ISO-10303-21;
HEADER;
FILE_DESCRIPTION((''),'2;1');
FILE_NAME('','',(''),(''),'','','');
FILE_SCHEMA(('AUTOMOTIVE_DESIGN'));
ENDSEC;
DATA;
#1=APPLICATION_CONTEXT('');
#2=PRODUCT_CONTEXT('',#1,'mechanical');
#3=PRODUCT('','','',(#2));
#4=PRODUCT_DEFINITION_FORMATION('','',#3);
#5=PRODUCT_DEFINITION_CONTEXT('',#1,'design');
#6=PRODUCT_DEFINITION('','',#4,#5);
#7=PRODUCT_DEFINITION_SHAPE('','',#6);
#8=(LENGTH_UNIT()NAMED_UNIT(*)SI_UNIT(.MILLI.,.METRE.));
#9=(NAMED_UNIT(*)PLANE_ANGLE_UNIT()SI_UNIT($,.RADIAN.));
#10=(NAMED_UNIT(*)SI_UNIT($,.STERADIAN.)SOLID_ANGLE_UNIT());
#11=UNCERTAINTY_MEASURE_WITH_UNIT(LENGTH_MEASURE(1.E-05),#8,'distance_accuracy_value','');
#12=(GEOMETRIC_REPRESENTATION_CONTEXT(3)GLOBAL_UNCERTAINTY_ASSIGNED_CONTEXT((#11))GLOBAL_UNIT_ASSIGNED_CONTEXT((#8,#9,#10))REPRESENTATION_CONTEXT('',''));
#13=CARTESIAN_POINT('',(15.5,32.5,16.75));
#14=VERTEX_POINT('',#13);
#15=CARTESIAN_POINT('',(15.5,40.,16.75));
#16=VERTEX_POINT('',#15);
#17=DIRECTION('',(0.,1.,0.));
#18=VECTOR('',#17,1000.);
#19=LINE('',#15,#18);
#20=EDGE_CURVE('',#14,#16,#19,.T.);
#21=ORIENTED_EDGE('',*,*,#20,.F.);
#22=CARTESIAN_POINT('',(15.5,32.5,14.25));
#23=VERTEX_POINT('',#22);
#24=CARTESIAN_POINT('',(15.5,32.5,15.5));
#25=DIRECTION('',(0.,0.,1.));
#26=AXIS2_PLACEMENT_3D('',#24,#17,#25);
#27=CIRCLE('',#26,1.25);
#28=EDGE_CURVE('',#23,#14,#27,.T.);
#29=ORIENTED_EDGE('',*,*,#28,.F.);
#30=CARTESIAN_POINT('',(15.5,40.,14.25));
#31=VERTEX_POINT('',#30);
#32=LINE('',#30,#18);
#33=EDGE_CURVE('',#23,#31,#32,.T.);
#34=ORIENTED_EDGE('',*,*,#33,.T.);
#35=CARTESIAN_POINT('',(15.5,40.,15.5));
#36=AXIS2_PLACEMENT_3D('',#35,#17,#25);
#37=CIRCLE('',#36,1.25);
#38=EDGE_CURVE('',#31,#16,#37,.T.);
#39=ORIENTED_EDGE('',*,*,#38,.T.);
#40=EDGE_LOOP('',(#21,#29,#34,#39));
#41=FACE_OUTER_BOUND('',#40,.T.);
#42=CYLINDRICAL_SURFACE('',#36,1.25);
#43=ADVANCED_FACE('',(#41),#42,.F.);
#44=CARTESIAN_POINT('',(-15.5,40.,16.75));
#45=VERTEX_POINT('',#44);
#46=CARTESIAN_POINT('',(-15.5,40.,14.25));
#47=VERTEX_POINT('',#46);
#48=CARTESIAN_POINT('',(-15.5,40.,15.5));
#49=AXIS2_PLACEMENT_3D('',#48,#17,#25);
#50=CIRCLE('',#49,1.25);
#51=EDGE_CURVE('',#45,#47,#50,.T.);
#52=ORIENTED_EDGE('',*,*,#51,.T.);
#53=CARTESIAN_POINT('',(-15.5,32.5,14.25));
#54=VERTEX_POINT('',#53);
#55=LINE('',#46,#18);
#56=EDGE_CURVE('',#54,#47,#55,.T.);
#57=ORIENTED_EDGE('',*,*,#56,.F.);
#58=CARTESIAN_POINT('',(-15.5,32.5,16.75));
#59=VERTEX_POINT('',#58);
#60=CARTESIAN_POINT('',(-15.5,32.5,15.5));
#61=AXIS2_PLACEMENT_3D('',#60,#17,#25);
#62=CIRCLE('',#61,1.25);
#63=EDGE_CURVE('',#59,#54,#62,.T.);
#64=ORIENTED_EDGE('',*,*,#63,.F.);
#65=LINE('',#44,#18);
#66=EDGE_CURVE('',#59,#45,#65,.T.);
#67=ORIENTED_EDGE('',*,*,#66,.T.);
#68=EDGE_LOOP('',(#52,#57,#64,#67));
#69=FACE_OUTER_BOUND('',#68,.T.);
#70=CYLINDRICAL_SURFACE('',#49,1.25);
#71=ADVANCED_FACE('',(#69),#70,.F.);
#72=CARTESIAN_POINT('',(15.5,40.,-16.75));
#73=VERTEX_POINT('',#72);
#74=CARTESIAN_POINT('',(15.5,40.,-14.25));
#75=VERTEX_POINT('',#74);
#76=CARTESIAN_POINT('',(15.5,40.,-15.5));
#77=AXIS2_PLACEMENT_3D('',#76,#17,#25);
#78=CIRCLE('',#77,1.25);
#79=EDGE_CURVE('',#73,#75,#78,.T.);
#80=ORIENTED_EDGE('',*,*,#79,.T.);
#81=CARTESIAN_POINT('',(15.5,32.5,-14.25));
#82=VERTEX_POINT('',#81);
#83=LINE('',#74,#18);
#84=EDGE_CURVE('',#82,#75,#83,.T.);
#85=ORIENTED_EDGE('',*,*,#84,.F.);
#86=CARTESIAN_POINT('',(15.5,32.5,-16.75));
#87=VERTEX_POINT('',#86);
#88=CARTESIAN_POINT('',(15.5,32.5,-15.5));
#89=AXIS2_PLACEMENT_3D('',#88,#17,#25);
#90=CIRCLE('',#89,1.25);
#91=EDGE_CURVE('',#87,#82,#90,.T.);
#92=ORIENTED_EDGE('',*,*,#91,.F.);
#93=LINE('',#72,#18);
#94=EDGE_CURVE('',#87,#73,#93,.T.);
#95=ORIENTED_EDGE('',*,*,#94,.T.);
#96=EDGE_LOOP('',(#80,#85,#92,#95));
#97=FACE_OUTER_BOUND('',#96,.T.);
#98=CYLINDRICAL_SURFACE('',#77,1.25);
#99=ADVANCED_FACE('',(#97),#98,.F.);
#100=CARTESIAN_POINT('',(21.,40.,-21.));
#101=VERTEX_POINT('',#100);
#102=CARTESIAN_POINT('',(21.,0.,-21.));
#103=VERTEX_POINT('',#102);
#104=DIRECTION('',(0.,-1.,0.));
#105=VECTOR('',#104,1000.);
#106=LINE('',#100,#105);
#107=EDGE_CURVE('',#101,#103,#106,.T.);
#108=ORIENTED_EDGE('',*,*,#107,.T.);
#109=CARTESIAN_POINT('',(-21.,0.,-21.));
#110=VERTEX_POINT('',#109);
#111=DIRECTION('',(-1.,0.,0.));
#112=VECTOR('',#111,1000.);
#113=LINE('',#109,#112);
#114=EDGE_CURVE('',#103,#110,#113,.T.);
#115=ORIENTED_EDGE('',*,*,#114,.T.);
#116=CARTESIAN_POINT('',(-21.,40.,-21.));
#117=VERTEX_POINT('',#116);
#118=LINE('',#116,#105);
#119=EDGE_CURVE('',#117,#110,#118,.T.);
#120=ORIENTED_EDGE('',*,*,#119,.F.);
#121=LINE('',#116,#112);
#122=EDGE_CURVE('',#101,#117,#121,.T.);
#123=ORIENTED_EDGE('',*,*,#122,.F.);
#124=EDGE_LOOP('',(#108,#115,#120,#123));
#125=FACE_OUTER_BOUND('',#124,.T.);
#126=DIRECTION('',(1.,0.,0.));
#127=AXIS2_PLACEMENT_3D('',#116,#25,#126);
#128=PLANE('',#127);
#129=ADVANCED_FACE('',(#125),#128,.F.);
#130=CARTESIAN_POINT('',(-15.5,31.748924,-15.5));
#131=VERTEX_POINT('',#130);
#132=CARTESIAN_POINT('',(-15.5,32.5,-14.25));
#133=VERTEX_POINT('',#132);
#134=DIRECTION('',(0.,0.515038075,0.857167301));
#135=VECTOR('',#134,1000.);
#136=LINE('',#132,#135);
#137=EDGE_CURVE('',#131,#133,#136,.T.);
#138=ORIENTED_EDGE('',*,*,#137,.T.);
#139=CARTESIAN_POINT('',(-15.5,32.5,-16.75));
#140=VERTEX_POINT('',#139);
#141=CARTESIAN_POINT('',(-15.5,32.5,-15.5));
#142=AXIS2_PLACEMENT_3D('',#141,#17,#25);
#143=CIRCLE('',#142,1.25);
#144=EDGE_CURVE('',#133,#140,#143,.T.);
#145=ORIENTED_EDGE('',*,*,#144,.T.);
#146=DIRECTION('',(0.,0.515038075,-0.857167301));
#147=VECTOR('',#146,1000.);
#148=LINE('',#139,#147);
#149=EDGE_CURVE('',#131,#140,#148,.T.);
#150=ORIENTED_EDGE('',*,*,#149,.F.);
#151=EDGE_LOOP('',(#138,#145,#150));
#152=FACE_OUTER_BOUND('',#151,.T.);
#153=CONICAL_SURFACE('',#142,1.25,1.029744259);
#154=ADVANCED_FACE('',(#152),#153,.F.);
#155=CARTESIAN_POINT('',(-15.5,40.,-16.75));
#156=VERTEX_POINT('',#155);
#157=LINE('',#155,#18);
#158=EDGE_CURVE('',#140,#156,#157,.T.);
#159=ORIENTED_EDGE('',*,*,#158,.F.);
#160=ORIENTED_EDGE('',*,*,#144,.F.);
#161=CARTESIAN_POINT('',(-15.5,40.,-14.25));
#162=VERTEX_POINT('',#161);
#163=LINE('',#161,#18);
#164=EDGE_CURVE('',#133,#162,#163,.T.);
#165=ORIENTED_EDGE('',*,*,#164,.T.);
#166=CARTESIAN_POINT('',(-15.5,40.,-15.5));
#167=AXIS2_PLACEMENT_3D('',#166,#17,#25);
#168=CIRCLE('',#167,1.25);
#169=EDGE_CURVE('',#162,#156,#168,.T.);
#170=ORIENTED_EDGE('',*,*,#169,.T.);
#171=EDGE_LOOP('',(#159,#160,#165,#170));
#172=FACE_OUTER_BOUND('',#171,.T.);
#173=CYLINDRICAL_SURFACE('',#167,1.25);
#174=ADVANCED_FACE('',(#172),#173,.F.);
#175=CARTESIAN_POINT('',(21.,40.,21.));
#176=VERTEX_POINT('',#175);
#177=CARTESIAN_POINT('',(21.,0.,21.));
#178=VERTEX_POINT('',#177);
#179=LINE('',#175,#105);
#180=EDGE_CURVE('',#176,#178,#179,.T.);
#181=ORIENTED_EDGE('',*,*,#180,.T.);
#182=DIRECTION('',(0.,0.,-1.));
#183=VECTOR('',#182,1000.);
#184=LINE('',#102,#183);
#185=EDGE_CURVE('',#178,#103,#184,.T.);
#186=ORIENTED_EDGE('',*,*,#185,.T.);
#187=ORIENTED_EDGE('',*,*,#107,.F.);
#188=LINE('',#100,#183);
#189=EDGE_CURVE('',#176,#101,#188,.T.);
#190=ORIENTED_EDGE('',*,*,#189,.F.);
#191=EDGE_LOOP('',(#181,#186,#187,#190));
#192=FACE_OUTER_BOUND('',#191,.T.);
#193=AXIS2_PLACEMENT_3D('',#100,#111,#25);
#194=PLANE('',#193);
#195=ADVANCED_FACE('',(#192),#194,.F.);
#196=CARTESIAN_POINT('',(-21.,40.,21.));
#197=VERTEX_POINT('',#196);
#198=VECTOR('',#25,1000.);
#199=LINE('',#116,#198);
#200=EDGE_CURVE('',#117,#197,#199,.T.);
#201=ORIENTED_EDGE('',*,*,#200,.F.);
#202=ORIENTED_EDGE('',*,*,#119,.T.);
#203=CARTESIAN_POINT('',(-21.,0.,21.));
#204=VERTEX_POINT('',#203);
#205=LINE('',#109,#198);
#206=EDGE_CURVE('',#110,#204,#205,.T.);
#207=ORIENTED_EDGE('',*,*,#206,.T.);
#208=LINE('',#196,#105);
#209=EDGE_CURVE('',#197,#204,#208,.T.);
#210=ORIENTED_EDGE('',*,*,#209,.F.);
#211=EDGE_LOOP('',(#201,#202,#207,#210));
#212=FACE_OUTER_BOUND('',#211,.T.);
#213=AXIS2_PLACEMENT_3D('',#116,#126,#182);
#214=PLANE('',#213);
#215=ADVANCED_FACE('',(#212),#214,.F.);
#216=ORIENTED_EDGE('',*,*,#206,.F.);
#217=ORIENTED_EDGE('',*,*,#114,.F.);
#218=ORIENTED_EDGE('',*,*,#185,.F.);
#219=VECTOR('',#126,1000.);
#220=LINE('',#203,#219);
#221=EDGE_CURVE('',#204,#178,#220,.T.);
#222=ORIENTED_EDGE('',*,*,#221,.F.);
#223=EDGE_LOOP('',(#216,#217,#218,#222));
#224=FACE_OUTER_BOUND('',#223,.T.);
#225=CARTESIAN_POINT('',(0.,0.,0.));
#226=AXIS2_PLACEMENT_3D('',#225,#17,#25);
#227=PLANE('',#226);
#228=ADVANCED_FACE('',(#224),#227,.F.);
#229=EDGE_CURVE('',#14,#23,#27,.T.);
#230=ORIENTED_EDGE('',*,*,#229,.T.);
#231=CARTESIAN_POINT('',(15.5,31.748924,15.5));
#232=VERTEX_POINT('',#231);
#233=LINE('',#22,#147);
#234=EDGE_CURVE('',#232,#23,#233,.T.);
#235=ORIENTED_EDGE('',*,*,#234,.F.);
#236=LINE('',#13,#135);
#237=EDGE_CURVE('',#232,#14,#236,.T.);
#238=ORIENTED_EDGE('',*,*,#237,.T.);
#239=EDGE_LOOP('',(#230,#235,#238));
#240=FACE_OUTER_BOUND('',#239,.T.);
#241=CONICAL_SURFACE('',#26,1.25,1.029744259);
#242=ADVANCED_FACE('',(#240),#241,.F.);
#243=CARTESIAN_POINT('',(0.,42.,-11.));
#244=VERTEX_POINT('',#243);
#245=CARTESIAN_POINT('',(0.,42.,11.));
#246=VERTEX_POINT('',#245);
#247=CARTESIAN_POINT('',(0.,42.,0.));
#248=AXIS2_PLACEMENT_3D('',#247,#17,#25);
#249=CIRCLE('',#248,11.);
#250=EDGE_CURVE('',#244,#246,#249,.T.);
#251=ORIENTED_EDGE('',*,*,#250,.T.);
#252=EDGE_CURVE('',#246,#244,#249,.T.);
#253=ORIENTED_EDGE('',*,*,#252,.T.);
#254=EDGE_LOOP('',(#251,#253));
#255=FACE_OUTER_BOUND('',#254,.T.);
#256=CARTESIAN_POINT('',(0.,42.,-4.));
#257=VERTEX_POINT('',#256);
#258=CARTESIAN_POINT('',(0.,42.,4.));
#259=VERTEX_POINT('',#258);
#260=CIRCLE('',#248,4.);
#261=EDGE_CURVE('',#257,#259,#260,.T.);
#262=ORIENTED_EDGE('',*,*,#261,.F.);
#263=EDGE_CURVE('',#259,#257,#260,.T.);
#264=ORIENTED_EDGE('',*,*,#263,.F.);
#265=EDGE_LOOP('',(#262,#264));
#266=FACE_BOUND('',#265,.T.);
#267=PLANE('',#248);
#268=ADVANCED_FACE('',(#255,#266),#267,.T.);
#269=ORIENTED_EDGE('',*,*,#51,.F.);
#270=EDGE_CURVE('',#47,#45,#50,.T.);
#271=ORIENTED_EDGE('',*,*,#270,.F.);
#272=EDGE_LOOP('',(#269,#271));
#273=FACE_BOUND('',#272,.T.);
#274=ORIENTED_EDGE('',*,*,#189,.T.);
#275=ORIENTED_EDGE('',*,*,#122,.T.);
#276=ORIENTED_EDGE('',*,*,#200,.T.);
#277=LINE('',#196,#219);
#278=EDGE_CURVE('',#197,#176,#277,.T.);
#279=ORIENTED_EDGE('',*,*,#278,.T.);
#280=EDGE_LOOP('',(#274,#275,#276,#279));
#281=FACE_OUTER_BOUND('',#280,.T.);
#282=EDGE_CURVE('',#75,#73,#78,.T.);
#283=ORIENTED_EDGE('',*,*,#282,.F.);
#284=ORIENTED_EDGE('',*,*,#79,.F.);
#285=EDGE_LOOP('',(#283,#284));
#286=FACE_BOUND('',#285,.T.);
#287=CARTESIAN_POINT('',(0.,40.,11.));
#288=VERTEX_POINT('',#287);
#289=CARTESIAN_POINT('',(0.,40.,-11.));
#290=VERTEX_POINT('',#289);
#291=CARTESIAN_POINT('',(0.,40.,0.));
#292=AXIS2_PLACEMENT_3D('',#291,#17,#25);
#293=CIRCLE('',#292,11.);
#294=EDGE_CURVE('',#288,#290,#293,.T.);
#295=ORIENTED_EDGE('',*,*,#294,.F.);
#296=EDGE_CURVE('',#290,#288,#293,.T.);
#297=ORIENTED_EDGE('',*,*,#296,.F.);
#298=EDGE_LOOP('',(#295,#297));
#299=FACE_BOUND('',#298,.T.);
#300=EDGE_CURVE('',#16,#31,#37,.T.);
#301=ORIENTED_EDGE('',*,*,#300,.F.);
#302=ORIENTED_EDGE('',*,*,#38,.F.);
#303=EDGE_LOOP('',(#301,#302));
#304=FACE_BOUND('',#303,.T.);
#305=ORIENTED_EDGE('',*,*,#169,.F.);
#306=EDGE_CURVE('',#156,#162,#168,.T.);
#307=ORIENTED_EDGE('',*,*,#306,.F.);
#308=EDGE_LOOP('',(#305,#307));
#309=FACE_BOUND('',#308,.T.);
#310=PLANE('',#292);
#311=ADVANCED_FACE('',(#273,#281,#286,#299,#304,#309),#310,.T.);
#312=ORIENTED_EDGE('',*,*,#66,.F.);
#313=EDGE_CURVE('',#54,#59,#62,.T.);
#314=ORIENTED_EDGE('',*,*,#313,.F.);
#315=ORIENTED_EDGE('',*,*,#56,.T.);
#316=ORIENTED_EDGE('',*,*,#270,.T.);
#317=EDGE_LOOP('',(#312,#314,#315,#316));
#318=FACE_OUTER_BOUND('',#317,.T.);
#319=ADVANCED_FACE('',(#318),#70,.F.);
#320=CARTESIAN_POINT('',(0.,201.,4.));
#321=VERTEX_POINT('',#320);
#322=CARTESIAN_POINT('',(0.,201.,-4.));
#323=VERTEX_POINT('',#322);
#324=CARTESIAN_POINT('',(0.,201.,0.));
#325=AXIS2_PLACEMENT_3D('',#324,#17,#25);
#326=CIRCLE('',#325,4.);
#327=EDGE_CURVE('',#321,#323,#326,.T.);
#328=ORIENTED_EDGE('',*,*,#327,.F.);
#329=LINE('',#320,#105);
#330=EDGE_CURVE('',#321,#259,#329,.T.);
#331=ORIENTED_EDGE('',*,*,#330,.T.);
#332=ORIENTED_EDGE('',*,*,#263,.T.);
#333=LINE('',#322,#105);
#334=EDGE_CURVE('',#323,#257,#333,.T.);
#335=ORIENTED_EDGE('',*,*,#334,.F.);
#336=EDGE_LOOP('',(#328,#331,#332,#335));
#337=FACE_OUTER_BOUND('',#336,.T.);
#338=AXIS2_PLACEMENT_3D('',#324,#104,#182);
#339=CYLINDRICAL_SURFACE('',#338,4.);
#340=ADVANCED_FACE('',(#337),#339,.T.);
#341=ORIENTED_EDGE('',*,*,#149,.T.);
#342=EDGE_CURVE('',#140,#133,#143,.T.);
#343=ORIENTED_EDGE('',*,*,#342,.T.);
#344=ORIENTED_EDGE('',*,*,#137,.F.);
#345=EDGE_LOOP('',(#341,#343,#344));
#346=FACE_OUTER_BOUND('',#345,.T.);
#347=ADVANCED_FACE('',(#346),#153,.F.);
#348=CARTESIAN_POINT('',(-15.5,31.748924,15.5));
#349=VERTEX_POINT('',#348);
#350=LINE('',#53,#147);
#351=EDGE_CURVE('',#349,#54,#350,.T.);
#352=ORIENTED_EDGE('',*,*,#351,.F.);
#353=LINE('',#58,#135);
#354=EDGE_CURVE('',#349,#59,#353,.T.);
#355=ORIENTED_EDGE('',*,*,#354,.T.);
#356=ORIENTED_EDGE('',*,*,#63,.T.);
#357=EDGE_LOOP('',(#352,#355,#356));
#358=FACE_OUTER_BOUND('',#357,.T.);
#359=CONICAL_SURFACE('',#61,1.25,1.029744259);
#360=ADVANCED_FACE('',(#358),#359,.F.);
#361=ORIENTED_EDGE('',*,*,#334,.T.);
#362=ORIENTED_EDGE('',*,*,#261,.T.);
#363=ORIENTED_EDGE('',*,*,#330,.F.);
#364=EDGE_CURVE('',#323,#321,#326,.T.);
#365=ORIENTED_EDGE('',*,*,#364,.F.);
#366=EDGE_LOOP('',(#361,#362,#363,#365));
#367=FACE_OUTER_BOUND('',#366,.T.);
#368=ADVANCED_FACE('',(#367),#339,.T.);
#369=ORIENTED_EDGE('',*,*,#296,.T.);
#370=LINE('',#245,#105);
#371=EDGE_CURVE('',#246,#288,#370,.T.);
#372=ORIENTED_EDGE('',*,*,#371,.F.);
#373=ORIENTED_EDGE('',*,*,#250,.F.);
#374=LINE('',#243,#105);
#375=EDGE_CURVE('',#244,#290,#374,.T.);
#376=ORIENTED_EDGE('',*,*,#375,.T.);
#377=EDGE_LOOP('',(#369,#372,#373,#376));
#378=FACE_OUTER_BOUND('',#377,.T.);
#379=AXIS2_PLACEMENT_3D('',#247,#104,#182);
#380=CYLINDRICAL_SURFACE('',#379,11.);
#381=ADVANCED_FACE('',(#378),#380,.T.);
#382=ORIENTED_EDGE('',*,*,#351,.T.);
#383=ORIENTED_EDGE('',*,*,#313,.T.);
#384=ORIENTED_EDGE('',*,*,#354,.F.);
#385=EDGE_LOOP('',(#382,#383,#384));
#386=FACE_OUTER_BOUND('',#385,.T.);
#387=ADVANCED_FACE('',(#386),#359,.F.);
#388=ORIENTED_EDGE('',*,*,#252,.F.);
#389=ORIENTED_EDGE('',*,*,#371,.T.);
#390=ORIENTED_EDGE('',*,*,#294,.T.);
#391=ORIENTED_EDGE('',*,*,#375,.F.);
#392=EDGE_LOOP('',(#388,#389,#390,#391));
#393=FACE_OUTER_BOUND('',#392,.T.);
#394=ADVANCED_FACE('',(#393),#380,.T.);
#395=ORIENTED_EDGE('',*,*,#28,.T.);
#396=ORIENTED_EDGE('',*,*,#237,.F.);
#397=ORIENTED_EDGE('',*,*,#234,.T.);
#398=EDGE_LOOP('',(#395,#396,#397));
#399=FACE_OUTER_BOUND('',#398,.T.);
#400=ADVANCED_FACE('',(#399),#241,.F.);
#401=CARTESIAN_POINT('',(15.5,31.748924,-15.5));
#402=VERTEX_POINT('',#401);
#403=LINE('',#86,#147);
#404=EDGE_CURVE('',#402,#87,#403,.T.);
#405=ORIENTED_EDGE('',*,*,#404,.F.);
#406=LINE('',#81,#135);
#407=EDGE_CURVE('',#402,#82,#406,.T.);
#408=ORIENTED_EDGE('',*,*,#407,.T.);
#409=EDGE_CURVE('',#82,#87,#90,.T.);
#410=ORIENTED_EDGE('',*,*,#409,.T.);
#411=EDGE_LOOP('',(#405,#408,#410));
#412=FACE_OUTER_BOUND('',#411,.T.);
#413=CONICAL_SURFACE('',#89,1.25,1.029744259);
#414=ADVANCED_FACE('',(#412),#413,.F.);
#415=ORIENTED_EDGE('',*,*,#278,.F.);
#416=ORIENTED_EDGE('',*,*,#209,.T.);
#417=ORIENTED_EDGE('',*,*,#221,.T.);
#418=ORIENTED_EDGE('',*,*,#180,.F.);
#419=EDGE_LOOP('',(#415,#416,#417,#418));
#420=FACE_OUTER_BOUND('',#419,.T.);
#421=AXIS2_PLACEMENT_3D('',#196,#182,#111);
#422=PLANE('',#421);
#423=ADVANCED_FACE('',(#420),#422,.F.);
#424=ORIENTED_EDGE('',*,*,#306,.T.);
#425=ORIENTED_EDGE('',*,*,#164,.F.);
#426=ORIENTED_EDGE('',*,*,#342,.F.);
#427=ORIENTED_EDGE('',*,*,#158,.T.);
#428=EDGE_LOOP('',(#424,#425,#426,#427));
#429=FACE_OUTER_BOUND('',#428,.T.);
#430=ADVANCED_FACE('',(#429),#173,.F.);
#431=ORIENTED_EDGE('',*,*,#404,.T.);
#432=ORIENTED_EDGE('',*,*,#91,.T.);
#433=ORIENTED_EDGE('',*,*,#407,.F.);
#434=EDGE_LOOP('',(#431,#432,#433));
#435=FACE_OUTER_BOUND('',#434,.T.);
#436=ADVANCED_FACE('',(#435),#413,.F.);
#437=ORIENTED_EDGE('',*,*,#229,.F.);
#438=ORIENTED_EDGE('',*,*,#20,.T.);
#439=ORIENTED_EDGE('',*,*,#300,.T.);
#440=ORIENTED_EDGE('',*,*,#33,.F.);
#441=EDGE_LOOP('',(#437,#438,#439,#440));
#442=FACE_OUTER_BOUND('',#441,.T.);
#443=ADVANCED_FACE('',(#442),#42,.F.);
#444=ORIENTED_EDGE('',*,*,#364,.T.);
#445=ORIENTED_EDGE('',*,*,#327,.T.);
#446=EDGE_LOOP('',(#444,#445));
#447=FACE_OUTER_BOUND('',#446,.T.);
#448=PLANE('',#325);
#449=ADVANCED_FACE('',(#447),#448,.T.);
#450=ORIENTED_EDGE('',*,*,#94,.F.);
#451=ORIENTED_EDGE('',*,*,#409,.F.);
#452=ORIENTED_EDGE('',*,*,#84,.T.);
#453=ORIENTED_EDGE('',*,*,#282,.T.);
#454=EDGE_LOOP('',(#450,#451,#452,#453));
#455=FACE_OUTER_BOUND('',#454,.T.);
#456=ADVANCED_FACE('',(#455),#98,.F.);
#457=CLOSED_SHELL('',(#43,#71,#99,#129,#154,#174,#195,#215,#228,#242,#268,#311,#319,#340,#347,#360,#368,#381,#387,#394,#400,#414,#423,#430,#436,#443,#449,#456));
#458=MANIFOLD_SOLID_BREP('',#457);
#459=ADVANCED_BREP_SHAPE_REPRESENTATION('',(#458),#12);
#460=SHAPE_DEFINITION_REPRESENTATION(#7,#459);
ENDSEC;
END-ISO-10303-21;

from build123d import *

# Parameters (mm, degrees)
SKETCH1_W             = 42
SKETCH1_H             = 42
BOSS_EXTRUDE1_DEPTH   = 40
SKETCH2_R             = 11
BOSS_EXTRUDE2_DEPTH   = 2
SKETCH3_R             = 4
BOSS_EXTRUDE3_DEPTH   = 159
SKETCH4_R             = 0.75
CUT_EXTRUDE1_DEPTH    = 5
M3_TAPPED_HOLE1_D     = 2.5
M3_TAPPED_HOLE1_DEPTH = 7.5
M3_TAPPED_HOLE1_TIP   = 0.751075774


with BuildPart() as part:
    # Sketch1 → Boss-Extrude1 (new body)
    with BuildSketch(Plane(origin=(0, 0, 0), x_dir=(1, 0, 0), z_dir=(0, 1, 0))):
        Rectangle(SKETCH1_W, SKETCH1_H)
    extrude(amount=BOSS_EXTRUDE1_DEPTH)

    # Sketch2 → Boss-Extrude2 (add)
    with BuildSketch(Plane(origin=(0, 40, 0), x_dir=(1, 0, 0), z_dir=(0, 1, 0))):
        with Locations(Location((0, 0, 0), (0, 0, 270))):
            Circle(SKETCH2_R)
    extrude(amount=BOSS_EXTRUDE2_DEPTH)

    # Sketch3 → Boss-Extrude3 (add)
    with BuildSketch(Plane(origin=(0, 42, 0), x_dir=(1, 0, 0), z_dir=(0, 1, 0))):
        with Locations(Location((0, 0, 0), (0, 0, 90))):
            Circle(SKETCH3_R)
    extrude(amount=BOSS_EXTRUDE3_DEPTH)

    # Sketch4 → Cut-Extrude1 (cut)
    with BuildSketch(Plane(origin=(0, 40, 0), x_dir=(1, 0, 0), z_dir=(0, 1, 0))):
        with Locations(Location((-15.5, 15.5, 0), (0, 0, 270))):
            Circle(SKETCH4_R)
        with Locations(Location((15.5, 15.5, 0), (0, 0, 270))):
            Circle(SKETCH4_R)
        with Locations(Location((15.5, -15.5, 0), (0, 0, 270))):
            Circle(SKETCH4_R)
        with Locations(Location((-15.5, -15.5, 0), (0, 0, 270))):
            Circle(SKETCH4_R)
    extrude(amount=-CUT_EXTRUDE1_DEPTH, mode=Mode.SUBTRACT)

    # M3 Tapped Hole1
    with Locations(Plane(origin=(0, 40, 0), x_dir=(1, 0, 0), z_dir=(0, 1, 0))):
        with Locations((-15.5, 15.5), (15.5, -15.5), (-15.5, -15.5), (15.5, 15.5)):
            Hole(M3_TAPPED_HOLE1_D / 2, depth=M3_TAPPED_HOLE1_DEPTH)
            with Locations((0, 0, -(M3_TAPPED_HOLE1_DEPTH + M3_TAPPED_HOLE1_TIP / 2))):  # 118° drill point
                Cone(0, M3_TAPPED_HOLE1_D / 2, M3_TAPPED_HOLE1_TIP, mode=Mode.SUBTRACT)


solid = part.part
